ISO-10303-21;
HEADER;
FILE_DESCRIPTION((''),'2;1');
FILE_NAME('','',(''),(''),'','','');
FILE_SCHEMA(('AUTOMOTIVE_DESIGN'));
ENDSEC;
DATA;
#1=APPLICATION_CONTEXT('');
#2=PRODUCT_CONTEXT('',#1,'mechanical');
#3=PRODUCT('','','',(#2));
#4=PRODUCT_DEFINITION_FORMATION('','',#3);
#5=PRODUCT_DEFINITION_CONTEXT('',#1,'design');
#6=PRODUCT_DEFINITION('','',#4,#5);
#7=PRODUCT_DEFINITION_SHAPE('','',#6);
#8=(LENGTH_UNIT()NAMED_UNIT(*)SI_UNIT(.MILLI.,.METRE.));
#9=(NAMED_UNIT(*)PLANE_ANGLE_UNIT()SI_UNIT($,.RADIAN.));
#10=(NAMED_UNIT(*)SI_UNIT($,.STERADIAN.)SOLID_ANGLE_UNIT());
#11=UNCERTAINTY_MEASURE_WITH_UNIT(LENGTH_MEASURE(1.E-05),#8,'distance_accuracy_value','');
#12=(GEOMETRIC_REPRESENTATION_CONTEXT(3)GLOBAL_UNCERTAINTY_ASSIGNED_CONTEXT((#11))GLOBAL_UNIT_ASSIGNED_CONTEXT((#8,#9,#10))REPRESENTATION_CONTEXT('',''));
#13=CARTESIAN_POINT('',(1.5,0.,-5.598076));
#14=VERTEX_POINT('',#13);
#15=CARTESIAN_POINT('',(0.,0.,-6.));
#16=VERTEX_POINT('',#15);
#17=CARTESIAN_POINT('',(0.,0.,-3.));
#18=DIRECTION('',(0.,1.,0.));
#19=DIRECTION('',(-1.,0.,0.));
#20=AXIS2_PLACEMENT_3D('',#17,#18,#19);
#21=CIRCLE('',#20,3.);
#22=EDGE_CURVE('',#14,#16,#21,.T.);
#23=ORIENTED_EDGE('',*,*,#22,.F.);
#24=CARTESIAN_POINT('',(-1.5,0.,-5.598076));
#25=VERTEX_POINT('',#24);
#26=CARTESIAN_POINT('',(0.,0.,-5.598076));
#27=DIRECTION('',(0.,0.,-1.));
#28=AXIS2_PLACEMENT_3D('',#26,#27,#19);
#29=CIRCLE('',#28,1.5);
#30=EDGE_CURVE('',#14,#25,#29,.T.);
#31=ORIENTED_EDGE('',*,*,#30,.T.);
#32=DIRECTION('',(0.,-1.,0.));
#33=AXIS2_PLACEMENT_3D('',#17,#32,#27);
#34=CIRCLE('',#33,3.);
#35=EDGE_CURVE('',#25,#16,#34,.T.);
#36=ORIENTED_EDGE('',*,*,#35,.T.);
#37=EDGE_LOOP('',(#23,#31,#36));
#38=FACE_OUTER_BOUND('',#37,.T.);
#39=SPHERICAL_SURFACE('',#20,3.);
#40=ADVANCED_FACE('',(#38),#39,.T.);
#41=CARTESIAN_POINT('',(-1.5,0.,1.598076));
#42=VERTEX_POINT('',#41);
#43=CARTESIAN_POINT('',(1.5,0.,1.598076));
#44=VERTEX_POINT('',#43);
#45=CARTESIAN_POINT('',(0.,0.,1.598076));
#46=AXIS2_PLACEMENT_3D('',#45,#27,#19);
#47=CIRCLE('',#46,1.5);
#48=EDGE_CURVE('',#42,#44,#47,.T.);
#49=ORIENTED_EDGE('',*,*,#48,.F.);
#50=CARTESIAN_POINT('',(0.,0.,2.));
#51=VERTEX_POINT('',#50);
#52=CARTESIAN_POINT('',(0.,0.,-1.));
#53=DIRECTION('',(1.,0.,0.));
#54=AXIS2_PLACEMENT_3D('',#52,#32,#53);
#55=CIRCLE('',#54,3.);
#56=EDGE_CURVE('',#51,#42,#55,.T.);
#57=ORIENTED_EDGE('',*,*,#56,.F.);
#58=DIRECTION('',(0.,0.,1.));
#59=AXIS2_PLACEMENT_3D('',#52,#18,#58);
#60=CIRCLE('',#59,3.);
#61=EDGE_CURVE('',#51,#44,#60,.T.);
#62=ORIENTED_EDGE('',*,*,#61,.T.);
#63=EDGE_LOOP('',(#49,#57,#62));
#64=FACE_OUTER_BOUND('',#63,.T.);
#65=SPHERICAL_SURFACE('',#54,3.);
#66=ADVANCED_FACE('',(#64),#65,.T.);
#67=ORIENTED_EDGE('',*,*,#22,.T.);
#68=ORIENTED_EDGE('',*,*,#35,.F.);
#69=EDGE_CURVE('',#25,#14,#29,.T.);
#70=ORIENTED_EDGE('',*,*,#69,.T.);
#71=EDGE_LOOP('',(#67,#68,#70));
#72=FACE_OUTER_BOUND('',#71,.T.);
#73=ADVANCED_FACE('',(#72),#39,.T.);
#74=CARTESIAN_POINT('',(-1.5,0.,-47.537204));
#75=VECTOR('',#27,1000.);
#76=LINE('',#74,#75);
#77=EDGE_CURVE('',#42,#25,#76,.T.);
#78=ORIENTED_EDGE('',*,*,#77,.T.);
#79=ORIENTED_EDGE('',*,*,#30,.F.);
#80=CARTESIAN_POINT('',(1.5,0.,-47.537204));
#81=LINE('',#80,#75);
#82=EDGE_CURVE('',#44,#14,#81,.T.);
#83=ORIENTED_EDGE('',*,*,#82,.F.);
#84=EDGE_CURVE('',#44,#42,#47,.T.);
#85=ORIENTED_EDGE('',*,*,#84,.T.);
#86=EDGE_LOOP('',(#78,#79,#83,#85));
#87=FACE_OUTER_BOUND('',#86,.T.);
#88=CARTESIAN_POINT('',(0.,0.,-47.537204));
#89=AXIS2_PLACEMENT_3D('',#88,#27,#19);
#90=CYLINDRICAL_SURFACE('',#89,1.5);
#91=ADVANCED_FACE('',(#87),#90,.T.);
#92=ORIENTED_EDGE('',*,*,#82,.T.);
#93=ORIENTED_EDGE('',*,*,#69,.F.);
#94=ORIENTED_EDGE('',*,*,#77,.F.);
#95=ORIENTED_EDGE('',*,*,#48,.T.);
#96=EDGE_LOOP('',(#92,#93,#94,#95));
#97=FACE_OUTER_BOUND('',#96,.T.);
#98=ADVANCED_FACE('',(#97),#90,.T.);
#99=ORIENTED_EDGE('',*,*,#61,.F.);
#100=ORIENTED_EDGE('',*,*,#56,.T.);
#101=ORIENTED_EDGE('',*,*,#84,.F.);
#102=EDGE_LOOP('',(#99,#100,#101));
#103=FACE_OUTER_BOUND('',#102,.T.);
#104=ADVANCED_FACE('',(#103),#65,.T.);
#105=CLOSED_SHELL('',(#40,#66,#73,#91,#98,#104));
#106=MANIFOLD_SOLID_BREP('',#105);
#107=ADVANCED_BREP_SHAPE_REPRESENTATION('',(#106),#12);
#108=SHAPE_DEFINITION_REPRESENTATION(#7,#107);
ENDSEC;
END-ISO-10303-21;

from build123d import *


with BuildPart() as part:
    # Logo3_bib1 → Revolve1 (revolve)
    with BuildSketch(Plane(origin=(0, 0, 0), x_dir=(-1, 0, 0), z_dir=(0, -1, 0))):
        with BuildLine():
            Line((0, 6), (0, -2))
            ThreePointArc((0, -2), (0.776457135, -1.897777479), (1.5, -1.598076211))
            Line((1.5, -1.598076211), (1.5, 5.598076211))
            ThreePointArc((1.5, 5.598076211), (0.776457135, 5.897777479), (0, 6))
        make_face()
    revolve(axis=Axis((0, 0, -47.537203702), (0, 0, 1)))


solid = part.part
